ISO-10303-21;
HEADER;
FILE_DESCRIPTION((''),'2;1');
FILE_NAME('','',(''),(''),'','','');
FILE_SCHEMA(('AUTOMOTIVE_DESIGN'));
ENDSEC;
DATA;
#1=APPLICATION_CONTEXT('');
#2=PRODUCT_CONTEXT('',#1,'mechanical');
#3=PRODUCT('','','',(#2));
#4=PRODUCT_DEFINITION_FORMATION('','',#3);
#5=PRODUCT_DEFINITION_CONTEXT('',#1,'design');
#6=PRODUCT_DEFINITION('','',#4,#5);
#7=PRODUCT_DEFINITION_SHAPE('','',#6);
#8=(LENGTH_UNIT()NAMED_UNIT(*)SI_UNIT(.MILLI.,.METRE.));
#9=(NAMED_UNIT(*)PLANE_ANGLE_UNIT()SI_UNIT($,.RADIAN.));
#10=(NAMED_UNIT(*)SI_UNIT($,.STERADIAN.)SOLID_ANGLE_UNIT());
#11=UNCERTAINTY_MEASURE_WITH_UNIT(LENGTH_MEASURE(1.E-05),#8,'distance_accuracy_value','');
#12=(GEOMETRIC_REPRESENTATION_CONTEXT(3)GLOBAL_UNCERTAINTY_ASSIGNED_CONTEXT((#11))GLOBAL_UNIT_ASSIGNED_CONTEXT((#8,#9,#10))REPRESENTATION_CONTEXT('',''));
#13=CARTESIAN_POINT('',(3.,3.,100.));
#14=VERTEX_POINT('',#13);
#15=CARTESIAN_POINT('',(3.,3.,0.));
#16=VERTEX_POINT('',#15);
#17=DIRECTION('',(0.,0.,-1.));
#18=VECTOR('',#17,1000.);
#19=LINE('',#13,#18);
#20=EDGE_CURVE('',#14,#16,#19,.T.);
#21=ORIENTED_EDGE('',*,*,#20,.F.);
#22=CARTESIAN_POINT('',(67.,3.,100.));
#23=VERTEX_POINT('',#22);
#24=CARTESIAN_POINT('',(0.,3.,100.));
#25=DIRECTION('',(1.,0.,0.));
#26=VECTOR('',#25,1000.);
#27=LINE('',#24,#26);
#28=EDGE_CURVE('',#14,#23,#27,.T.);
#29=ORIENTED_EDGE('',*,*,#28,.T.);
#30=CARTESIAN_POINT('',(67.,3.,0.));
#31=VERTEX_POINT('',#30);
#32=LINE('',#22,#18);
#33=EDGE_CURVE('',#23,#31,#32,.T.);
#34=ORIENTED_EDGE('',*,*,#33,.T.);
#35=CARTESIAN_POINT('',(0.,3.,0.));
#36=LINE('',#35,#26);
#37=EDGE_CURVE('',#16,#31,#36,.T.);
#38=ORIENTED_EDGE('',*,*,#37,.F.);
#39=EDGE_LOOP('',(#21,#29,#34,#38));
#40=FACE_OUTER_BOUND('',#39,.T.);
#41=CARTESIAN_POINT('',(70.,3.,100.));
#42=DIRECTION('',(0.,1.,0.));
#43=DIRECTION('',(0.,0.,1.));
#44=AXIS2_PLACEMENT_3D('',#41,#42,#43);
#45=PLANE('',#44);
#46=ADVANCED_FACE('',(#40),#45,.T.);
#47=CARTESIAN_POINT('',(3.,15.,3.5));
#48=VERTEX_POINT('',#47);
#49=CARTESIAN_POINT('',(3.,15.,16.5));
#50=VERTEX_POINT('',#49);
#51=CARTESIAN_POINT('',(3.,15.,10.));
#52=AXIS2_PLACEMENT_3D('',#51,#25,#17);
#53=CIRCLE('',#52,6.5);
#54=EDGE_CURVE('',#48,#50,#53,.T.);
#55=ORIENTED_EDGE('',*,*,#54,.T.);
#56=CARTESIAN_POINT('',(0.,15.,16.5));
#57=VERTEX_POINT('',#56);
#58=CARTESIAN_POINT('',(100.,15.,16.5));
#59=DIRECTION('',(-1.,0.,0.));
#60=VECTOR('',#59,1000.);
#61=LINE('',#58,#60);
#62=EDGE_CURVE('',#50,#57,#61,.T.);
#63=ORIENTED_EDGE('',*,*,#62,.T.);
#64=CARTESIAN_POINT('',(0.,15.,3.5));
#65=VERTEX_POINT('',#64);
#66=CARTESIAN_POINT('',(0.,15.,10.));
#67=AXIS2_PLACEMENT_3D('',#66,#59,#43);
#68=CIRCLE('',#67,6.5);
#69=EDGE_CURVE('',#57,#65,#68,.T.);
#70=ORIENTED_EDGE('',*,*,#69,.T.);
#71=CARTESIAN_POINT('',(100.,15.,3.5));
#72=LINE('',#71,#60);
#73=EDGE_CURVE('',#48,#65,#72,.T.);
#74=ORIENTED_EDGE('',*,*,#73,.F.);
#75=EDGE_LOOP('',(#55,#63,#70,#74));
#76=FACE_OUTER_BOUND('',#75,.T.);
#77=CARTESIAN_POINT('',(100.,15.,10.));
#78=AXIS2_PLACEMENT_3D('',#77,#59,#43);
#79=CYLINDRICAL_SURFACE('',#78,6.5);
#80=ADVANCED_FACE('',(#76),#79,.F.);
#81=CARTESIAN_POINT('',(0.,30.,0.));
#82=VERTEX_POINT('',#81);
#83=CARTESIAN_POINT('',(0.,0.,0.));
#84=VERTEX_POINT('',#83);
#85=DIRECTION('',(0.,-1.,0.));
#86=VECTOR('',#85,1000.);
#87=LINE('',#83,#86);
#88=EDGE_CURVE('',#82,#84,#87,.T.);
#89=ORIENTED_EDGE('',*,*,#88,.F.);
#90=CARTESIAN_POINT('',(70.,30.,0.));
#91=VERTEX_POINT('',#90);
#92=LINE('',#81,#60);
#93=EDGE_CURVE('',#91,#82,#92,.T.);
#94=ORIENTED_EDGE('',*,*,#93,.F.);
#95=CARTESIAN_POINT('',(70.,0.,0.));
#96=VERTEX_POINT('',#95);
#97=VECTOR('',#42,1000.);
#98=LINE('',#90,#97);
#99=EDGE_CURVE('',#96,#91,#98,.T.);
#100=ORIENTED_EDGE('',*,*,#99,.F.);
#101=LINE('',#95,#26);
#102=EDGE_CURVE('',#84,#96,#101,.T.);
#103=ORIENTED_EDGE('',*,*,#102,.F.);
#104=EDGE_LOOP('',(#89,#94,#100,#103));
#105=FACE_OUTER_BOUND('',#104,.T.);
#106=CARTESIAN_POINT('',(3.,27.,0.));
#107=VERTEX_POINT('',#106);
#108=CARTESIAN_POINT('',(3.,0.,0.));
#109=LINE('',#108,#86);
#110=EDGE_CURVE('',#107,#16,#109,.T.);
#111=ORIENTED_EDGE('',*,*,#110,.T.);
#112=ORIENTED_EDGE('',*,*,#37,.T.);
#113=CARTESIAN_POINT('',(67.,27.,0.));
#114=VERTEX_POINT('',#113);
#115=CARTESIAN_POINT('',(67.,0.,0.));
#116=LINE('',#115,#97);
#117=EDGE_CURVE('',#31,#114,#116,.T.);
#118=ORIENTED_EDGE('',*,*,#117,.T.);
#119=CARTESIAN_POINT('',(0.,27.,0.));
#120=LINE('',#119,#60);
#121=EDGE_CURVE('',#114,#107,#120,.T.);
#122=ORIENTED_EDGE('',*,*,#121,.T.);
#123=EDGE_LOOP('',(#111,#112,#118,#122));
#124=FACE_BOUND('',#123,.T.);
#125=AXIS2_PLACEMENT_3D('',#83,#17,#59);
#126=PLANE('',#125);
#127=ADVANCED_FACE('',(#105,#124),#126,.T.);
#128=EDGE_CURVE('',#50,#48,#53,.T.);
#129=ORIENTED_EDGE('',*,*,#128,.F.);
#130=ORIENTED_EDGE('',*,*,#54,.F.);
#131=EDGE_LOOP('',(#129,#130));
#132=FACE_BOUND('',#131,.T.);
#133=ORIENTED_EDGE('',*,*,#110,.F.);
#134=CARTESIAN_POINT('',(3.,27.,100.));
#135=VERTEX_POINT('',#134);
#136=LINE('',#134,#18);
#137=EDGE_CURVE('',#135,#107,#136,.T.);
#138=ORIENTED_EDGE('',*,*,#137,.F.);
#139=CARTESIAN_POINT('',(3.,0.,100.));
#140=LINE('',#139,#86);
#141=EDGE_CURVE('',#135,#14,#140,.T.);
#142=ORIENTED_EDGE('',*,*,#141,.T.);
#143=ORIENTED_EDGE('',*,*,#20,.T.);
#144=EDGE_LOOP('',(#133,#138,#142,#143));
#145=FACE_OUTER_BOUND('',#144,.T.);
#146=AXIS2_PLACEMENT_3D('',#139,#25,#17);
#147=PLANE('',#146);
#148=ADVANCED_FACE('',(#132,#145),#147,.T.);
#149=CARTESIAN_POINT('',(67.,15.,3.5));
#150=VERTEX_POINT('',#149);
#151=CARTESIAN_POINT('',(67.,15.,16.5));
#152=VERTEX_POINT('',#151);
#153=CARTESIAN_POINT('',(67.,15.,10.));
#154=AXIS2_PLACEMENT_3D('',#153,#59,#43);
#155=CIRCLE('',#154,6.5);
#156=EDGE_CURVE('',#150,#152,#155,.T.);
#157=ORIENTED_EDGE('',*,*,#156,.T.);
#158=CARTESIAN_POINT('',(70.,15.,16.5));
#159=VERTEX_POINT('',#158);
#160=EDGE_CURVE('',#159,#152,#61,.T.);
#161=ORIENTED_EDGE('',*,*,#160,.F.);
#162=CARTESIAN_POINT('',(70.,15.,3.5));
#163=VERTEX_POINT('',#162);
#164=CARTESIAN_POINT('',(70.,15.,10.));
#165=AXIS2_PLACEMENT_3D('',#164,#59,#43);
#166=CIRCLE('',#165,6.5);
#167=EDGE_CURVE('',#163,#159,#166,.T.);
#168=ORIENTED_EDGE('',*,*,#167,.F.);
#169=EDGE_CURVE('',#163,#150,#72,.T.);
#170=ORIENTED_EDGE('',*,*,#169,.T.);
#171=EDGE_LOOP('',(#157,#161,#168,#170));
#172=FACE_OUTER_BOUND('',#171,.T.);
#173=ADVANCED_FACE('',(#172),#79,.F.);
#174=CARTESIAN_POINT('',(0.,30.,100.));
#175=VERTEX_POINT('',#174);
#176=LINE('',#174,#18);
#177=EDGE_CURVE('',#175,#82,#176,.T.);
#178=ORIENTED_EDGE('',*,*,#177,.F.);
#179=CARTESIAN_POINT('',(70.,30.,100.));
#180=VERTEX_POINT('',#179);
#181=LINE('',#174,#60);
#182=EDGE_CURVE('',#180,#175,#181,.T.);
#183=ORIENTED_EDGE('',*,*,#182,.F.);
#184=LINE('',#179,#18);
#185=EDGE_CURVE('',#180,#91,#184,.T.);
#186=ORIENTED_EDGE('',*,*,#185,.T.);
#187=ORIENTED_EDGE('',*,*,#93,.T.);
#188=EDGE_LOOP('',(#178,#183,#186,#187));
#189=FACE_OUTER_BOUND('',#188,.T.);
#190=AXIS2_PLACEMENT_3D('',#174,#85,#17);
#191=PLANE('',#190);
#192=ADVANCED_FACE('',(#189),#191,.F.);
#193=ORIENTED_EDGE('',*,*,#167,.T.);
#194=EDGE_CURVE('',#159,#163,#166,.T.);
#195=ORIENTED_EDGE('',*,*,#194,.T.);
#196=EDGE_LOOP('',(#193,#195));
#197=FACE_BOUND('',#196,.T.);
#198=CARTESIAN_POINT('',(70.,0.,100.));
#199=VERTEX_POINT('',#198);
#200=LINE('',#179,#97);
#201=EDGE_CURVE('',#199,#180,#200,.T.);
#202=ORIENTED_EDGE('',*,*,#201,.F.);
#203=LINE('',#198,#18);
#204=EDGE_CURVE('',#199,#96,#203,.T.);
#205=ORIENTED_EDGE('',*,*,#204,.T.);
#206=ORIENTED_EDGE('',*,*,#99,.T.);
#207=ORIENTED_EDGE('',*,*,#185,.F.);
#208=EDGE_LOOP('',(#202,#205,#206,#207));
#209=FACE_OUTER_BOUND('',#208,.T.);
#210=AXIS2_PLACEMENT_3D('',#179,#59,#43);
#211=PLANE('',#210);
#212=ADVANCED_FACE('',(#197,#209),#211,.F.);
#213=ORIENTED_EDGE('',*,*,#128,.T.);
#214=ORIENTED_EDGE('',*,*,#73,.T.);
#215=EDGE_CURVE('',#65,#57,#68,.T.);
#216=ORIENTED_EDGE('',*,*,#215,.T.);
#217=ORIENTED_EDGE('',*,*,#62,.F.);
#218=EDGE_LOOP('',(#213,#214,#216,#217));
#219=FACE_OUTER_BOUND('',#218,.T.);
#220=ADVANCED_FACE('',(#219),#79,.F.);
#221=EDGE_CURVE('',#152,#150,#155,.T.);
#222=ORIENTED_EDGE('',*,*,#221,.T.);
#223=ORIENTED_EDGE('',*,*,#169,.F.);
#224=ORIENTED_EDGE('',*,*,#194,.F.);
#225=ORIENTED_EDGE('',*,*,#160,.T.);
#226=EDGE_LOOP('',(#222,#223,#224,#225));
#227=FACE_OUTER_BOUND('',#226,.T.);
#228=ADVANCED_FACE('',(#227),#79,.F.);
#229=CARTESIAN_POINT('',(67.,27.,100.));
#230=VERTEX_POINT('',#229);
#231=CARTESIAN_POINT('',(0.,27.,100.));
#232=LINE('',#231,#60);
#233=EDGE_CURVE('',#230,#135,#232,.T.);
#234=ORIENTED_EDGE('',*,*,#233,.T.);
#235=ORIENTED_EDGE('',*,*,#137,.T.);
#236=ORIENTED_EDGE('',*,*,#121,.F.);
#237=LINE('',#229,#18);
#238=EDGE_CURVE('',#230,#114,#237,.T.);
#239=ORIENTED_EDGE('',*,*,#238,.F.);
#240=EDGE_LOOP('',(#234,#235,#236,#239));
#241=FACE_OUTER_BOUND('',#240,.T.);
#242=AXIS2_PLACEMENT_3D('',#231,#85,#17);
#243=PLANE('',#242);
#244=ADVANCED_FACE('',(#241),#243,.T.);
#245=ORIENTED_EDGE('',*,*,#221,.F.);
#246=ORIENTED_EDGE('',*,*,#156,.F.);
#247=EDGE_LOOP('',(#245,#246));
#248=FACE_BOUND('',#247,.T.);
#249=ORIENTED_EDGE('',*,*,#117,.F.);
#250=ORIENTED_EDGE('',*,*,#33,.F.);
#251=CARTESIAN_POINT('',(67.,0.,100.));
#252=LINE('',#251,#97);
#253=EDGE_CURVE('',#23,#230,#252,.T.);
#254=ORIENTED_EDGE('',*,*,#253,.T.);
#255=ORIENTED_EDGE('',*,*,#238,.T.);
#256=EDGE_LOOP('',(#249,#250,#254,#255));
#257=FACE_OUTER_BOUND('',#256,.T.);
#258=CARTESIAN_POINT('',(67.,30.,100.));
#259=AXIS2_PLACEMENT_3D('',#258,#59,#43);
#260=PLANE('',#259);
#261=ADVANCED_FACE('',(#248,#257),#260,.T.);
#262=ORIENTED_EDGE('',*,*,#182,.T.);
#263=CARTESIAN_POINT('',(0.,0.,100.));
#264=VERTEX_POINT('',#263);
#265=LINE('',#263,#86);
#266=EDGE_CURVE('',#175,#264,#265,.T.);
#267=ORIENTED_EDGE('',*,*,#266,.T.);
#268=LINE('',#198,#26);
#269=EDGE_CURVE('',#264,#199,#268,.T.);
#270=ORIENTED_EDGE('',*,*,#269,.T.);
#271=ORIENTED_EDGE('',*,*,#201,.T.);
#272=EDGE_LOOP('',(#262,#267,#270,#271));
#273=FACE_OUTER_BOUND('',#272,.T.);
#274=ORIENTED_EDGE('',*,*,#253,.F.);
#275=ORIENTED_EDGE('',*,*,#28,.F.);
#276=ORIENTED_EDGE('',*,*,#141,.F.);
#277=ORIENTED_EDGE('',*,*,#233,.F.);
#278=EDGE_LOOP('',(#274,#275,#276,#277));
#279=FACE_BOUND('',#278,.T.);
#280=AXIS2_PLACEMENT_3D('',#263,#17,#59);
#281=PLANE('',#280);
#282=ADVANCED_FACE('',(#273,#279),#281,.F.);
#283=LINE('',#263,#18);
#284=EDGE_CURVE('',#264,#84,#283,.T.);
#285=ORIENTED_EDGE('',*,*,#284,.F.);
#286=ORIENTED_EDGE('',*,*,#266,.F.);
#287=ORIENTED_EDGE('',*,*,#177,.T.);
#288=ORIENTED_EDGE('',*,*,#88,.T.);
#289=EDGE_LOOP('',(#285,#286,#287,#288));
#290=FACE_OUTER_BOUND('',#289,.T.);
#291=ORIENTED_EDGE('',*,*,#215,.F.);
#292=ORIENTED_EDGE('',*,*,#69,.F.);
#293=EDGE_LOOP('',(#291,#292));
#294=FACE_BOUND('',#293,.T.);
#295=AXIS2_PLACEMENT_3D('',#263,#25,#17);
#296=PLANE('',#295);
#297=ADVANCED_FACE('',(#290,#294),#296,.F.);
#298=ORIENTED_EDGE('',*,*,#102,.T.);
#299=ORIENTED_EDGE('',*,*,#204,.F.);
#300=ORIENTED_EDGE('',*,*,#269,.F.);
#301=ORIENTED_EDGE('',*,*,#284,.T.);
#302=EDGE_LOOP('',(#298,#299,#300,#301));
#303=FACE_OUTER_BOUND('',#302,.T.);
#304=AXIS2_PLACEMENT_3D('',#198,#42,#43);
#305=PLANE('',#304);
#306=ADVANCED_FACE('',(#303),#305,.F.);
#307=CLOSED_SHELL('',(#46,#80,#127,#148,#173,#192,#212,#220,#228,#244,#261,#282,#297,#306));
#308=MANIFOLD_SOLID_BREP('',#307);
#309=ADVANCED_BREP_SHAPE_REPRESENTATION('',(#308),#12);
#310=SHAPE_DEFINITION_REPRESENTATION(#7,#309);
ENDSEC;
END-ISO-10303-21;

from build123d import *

# Parameters (mm, degrees)
SKETCH_1_W          = 70
SKETCH_1_H          = 30
EXTRUDE_1_DEPTH     = 100
SHELL_1_T           = -3
SKETCH_2_R          = 6.5
CUT_EXTRUDE_2_DEPTH = 100


with BuildPart() as part:
    # 草图1 → 凸台-拉伸1 (new body)
    with BuildSketch(Plane.XY):
        with Locations((35, 15)):
            Rectangle(SKETCH_1_W, SKETCH_1_H)
    extrude(amount=EXTRUDE_1_DEPTH)

    # 抽壳1
    shell_1_openings = [part.faces().sort_by_distance(p)[0] for p in [
        (35, 15, 100),
        (35, 15, 0),
    ]]
    offset(amount=SHELL_1_T, openings=shell_1_openings, kind=Kind.INTERSECTION)

    # 草图2 → 切除-拉伸2 (cut)
    with BuildSketch(Plane.ZY):
        with Locations((10, 15)):
            Circle(SKETCH_2_R)
    extrude(amount=-CUT_EXTRUDE_2_DEPTH, mode=Mode.SUBTRACT)


solid = part.part
